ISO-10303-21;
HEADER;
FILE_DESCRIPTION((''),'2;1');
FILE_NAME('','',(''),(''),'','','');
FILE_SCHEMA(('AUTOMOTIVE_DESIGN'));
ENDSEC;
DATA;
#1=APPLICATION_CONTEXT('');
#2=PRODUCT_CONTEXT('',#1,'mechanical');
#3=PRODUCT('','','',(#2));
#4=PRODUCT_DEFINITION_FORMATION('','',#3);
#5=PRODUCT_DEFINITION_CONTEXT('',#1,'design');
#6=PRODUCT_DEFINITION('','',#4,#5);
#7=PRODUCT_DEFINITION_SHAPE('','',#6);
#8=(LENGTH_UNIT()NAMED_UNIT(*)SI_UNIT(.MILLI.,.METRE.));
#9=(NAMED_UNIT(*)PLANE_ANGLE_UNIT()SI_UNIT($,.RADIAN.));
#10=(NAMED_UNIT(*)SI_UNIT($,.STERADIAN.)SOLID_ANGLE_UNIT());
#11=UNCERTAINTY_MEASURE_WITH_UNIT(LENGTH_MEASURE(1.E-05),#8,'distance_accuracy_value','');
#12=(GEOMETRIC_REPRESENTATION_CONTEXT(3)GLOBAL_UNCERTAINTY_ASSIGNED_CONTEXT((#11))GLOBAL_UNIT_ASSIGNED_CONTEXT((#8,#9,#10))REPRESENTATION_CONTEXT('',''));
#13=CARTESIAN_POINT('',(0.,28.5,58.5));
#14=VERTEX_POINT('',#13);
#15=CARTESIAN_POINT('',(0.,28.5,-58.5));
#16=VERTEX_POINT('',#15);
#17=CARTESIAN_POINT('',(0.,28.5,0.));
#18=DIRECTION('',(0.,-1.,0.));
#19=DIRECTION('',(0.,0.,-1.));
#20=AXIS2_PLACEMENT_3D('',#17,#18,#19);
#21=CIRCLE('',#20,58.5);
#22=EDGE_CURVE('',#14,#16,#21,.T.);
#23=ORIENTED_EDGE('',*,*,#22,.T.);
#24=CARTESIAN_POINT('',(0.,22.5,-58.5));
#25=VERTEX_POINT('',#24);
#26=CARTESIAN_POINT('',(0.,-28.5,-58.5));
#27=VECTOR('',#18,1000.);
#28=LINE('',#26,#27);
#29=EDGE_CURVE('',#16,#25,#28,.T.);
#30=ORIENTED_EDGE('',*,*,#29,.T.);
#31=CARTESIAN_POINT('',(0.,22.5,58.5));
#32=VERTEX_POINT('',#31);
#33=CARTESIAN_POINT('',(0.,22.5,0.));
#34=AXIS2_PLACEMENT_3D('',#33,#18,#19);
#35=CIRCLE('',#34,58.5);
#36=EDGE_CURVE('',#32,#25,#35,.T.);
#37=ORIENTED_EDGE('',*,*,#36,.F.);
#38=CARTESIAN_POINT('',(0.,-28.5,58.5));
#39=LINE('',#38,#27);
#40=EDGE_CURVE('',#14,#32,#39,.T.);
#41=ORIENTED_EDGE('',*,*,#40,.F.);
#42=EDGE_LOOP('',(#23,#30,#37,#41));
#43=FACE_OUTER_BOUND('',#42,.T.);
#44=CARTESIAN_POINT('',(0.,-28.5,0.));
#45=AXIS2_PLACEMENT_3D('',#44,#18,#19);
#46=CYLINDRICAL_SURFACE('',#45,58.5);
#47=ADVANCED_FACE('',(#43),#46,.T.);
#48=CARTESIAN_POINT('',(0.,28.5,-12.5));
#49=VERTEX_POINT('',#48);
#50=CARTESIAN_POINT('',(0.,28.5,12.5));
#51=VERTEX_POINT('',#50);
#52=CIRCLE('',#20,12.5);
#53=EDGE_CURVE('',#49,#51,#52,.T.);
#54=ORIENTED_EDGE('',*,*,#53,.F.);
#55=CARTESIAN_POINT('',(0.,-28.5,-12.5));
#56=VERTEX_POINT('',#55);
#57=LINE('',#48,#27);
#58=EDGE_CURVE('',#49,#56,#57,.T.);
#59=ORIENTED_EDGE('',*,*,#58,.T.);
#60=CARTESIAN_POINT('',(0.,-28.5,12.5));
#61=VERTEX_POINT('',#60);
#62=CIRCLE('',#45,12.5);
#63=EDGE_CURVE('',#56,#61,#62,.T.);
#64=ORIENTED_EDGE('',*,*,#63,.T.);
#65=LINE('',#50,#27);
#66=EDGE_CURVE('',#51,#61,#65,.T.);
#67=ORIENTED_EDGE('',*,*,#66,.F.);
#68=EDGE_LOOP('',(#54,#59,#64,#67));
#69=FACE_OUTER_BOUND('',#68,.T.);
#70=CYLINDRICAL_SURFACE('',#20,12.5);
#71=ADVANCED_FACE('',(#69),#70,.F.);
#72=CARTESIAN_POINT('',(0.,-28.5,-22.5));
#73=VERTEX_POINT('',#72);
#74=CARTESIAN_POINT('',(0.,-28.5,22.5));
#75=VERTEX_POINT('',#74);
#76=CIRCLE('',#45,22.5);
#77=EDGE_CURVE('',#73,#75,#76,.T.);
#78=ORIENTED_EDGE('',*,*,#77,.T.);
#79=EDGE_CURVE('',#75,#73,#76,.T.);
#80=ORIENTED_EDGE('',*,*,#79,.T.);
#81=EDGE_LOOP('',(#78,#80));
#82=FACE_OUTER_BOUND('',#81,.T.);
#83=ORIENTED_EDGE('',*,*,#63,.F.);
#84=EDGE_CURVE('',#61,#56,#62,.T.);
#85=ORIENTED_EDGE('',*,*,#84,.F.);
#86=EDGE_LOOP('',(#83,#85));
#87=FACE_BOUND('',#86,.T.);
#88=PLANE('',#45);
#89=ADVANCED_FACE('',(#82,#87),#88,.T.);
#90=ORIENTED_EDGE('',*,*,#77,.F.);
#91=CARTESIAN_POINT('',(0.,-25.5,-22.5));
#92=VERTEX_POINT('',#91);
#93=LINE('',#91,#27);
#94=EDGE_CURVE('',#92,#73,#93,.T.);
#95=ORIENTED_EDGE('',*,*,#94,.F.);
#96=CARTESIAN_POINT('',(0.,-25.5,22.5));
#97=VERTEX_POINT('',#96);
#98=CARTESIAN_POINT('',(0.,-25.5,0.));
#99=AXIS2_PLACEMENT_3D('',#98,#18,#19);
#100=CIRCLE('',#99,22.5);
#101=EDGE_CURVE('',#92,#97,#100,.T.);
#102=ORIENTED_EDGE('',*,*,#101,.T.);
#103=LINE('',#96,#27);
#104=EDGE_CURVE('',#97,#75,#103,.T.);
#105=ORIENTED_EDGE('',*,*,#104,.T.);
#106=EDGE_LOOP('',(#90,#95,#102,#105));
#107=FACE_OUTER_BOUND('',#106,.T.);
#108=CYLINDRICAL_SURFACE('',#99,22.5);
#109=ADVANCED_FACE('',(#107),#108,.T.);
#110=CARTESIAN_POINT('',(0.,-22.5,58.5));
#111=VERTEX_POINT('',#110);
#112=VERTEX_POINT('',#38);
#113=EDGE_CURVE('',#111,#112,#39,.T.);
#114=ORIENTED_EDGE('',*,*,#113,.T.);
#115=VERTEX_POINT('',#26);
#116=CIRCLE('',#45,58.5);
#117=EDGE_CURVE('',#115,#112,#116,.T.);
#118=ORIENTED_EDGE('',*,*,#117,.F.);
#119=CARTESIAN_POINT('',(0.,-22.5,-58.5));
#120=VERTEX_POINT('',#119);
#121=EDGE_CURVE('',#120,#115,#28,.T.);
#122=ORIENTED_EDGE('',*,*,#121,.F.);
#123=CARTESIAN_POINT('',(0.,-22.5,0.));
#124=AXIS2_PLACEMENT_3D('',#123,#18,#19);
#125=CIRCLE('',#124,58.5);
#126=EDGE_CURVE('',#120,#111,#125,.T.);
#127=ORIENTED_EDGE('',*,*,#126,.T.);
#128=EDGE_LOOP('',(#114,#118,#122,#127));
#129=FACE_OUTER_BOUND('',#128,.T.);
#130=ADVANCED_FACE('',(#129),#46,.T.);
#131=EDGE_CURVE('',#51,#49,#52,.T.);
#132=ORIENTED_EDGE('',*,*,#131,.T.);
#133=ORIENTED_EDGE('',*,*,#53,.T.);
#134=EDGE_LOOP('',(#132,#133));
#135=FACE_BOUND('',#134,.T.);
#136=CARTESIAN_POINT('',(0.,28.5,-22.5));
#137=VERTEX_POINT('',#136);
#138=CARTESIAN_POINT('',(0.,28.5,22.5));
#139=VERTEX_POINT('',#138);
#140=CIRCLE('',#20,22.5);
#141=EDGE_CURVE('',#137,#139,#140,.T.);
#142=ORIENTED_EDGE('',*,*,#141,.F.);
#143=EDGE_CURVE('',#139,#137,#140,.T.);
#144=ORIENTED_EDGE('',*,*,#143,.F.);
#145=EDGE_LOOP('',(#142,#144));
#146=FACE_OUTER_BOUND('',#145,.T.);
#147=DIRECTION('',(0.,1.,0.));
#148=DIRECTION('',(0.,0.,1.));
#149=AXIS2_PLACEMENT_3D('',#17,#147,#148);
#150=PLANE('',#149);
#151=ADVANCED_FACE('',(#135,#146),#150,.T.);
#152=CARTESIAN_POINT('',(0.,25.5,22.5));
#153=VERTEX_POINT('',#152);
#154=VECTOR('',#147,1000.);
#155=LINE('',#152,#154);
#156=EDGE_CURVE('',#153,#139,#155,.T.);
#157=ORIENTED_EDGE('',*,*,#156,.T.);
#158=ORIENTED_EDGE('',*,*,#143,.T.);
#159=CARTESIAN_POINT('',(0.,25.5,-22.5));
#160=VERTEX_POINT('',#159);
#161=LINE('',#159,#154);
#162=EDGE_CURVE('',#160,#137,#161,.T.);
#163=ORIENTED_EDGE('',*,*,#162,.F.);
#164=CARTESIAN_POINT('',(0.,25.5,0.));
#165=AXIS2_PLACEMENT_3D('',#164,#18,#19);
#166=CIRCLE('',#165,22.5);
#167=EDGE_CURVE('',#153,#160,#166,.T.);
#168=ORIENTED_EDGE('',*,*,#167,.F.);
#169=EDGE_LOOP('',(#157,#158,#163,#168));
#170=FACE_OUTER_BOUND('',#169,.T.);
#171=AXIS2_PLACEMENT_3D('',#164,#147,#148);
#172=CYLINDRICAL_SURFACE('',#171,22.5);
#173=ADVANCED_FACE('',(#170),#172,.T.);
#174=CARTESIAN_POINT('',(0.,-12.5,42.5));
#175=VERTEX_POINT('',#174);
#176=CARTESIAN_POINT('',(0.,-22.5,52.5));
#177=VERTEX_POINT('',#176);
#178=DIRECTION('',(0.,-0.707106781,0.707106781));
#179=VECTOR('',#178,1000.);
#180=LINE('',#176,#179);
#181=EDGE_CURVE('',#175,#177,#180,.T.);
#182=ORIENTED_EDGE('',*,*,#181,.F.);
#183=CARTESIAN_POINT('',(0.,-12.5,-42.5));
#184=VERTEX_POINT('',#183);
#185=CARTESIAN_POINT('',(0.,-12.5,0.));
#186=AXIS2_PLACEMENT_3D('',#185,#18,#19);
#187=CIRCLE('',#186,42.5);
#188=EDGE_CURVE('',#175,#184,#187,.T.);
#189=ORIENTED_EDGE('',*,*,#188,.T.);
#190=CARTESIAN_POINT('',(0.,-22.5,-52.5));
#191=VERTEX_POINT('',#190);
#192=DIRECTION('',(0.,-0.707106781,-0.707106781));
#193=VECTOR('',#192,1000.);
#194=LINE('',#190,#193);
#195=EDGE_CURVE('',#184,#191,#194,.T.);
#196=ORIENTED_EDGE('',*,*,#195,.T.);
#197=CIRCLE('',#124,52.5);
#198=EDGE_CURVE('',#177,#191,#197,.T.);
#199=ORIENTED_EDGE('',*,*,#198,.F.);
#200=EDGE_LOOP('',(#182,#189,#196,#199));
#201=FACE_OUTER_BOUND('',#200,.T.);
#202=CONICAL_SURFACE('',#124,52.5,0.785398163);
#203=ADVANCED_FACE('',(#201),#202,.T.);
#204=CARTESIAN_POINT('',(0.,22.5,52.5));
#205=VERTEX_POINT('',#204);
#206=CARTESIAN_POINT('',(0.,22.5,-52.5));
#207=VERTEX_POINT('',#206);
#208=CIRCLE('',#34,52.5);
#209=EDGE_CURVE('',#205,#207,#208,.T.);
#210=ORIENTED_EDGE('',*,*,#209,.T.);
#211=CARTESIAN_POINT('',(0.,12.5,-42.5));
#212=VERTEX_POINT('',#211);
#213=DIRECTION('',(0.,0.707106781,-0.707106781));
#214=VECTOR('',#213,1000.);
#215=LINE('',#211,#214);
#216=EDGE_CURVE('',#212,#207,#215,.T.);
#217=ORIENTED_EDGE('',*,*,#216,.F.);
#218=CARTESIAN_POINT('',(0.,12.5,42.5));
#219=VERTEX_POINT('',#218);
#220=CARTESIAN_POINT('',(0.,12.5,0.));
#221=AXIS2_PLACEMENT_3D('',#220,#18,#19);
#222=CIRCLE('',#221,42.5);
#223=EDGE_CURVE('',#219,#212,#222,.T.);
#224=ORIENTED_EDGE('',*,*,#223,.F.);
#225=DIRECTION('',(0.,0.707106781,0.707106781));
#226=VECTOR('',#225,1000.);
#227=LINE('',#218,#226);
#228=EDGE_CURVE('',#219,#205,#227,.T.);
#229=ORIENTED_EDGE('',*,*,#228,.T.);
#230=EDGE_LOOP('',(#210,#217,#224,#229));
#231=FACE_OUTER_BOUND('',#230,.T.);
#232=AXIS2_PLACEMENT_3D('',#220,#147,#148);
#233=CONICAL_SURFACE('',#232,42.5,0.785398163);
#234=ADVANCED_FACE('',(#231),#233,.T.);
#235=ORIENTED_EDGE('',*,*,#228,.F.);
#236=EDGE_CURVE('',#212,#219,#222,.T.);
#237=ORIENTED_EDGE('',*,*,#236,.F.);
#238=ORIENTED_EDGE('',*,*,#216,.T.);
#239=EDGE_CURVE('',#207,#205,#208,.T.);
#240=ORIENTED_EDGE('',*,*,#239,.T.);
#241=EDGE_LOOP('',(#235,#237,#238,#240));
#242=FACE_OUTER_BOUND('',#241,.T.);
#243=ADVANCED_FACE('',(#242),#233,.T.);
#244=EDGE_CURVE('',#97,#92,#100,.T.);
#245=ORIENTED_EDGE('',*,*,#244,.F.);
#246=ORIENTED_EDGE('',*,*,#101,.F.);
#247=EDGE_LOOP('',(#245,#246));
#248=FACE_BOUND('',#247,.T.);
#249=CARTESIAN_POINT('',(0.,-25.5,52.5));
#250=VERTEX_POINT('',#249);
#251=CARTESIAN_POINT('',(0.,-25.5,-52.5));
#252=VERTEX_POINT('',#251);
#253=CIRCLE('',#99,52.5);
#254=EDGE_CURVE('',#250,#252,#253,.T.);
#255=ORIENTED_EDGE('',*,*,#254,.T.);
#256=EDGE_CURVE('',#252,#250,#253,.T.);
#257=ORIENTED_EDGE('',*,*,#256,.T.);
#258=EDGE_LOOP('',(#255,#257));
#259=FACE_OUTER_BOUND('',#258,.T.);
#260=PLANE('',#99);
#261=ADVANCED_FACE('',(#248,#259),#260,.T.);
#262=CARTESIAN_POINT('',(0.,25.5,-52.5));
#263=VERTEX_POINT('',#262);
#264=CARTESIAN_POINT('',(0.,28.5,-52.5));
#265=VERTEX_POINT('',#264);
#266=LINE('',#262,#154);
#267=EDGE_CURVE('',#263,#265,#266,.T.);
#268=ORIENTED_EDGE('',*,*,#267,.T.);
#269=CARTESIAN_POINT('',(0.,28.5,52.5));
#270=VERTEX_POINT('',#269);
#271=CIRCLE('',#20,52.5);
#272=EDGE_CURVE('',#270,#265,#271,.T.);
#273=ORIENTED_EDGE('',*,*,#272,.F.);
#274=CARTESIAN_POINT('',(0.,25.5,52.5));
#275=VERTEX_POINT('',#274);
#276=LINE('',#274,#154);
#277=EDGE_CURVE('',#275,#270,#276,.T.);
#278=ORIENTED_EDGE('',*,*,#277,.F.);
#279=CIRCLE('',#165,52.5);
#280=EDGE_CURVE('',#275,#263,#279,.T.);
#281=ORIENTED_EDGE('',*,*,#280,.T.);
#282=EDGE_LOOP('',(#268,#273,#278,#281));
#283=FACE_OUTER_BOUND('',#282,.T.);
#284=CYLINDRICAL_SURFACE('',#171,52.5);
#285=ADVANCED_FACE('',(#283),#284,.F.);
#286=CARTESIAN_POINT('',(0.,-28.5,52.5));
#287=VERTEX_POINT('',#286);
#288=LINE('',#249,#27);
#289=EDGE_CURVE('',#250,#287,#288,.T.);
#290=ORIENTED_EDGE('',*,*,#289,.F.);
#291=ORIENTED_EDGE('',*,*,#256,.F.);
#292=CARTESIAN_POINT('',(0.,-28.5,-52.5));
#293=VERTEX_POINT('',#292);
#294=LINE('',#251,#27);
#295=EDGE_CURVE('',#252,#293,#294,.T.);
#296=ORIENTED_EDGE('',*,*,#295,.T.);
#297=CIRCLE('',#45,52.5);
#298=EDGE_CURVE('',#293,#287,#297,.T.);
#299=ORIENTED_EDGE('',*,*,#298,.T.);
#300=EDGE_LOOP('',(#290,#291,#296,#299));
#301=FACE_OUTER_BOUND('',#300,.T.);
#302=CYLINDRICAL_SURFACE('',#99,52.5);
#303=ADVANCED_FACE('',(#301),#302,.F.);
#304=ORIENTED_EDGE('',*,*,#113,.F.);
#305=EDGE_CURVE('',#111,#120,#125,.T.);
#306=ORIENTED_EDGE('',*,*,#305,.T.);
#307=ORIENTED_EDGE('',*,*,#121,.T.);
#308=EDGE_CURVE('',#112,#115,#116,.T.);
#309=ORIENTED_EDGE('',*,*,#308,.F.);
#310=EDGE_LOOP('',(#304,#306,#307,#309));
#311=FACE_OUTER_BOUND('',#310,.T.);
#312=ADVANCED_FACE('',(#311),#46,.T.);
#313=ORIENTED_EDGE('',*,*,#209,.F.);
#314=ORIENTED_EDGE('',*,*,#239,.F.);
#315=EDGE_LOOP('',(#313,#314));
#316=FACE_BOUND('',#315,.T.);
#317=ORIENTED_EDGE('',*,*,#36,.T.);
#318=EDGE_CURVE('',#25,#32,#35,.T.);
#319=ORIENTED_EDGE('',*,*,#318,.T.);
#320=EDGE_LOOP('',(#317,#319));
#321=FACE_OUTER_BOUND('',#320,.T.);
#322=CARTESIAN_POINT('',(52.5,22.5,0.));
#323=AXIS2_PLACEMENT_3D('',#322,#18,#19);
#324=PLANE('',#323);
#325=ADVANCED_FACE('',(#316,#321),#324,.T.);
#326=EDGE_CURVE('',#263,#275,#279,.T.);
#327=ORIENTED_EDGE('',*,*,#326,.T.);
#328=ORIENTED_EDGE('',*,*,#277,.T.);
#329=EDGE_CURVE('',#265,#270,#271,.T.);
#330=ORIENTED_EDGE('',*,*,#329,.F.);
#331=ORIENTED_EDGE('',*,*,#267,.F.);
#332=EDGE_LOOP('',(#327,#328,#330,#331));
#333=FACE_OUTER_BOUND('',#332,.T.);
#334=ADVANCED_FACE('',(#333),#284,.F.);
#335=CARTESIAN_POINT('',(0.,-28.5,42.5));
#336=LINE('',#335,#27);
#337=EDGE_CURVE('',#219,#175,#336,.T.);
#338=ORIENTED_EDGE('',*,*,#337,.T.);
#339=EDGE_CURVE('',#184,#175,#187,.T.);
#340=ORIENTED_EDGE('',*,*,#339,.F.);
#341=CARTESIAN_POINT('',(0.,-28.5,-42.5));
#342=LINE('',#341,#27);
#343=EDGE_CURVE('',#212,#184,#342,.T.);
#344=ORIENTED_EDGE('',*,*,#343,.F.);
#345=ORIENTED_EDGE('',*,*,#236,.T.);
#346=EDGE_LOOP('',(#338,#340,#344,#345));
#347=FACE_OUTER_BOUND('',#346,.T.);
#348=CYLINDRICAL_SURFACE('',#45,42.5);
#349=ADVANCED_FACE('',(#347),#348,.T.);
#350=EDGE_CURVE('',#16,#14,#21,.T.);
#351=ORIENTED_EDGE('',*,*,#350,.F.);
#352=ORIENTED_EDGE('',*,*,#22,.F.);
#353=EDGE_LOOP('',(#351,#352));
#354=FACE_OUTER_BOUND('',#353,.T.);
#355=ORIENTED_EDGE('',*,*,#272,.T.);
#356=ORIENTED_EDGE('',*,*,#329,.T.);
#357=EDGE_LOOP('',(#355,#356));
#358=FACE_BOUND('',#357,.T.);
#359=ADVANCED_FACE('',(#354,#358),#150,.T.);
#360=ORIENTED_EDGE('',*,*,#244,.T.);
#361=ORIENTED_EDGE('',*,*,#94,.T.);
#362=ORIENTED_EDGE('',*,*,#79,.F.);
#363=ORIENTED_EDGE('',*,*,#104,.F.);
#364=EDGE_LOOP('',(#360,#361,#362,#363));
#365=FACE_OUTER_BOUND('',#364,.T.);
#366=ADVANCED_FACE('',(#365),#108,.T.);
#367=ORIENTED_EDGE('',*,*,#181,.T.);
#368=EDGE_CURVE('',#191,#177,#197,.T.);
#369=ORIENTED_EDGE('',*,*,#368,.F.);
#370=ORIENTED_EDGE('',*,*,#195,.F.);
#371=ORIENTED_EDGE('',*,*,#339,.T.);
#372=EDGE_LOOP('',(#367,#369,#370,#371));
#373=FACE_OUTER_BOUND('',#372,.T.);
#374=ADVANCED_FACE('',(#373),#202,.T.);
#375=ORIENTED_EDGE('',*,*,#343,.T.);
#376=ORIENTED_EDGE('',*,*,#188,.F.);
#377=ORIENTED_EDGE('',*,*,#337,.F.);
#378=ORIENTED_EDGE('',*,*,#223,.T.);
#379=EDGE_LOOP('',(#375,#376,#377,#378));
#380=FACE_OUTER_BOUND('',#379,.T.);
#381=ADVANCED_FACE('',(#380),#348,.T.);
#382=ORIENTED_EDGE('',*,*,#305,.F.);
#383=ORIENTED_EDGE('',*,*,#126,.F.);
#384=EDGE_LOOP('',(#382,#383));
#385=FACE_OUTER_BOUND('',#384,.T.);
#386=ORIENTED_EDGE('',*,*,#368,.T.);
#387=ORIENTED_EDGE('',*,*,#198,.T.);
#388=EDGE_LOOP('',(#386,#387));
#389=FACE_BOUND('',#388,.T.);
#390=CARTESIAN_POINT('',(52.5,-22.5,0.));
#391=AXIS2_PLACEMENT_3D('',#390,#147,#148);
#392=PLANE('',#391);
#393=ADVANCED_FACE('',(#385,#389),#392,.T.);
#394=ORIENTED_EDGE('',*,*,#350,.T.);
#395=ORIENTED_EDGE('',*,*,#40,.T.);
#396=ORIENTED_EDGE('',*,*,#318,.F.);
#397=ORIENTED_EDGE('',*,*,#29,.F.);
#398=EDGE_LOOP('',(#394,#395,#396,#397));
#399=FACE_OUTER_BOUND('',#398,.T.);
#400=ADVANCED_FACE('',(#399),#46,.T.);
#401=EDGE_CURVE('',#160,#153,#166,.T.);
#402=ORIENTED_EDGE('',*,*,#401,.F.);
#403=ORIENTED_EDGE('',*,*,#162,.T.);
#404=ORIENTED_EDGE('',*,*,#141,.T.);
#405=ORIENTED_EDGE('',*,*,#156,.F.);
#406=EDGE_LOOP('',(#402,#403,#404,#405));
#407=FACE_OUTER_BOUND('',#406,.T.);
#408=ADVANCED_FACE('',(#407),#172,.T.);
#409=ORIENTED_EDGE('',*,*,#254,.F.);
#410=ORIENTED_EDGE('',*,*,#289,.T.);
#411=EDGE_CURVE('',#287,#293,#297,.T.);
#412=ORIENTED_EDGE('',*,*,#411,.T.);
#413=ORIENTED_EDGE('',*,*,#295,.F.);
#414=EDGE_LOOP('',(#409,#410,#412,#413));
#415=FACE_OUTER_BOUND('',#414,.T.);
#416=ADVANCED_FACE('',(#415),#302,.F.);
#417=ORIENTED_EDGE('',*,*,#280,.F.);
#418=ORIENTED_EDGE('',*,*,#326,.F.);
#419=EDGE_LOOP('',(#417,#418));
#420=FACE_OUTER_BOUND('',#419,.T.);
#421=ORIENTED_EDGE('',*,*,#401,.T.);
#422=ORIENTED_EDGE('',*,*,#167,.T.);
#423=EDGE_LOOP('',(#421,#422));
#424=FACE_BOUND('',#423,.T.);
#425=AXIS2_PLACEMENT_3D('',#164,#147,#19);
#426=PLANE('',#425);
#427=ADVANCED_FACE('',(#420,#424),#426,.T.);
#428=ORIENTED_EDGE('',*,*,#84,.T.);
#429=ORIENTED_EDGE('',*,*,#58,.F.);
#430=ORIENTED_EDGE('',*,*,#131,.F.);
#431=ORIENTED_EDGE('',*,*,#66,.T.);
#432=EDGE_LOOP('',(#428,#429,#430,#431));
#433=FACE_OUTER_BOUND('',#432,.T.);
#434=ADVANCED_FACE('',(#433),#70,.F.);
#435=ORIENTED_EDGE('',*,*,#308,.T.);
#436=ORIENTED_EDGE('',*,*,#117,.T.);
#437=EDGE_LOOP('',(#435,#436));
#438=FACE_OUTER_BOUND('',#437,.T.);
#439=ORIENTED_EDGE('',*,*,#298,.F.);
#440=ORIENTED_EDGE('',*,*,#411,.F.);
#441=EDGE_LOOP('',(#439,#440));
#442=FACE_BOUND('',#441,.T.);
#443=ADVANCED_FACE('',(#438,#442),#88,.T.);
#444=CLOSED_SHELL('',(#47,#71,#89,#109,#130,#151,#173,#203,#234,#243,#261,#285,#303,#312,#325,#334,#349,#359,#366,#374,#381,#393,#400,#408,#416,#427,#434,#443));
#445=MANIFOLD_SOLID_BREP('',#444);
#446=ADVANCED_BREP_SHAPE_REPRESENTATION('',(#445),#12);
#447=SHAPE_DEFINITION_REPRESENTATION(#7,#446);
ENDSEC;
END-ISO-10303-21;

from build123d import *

# Parameters (mm, degrees)
SKETCH_2_R          = 12.5
CUT_EXTRUDE_1_DEPTH = 101.466412298
SKETCH_3_R          = 52.5
SKETCH_3_R_2        = 22.5
CUT_EXTRUDE_2_DEPTH = 3


with BuildPart() as part:
    # 草图1 → 旋转1 (revolve)
    with BuildSketch(Plane.XY, mode=Mode.PRIVATE) as revolve_1_sk:
        Polygon((52.5, 22.5), (58.5, 22.5), (58.5, 28.5), (0, 28.5), (0, -28.5), (58.5, -28.5), (58.5, -22.5), (52.5, -22.5), (42.5, -12.5), (42.5, 12.5), align=None)
    revolve(revolve_1_sk.sketch.rotate(Axis((0, -28.5, 0), (0, 1, 0)), 90), axis=Axis((0, -28.5, 0), (0, 1, 0)))

    # 草图2 → 切除-拉伸1 (cut, through all)
    with BuildSketch(Plane.XZ.offset(28.5)):
        with Locations(Location((0, 0, 0), (0, 0, 270))):
            Circle(SKETCH_2_R)
    extrude(amount=-CUT_EXTRUDE_1_DEPTH, mode=Mode.SUBTRACT)

    # 草图3 → 切除-拉伸2 (cut)
    with BuildSketch(Plane.XZ.offset(28.5)):
        with Locations(Location((0, 0, 0), (0, 0, 270))):
            Circle(SKETCH_3_R)
        with Locations(Location((0, 0, 0), (0, 0, 270))):
            Circle(SKETCH_3_R_2, mode=Mode.SUBTRACT)
    cut_extrude_2 = extrude(amount=-CUT_EXTRUDE_2_DEPTH, mode=Mode.SUBTRACT)

    # 镜向1: 切除-拉伸2 across plane
    add(cut_extrude_2.mirror(Plane.ZX), mode=Mode.SUBTRACT)


solid = part.part
